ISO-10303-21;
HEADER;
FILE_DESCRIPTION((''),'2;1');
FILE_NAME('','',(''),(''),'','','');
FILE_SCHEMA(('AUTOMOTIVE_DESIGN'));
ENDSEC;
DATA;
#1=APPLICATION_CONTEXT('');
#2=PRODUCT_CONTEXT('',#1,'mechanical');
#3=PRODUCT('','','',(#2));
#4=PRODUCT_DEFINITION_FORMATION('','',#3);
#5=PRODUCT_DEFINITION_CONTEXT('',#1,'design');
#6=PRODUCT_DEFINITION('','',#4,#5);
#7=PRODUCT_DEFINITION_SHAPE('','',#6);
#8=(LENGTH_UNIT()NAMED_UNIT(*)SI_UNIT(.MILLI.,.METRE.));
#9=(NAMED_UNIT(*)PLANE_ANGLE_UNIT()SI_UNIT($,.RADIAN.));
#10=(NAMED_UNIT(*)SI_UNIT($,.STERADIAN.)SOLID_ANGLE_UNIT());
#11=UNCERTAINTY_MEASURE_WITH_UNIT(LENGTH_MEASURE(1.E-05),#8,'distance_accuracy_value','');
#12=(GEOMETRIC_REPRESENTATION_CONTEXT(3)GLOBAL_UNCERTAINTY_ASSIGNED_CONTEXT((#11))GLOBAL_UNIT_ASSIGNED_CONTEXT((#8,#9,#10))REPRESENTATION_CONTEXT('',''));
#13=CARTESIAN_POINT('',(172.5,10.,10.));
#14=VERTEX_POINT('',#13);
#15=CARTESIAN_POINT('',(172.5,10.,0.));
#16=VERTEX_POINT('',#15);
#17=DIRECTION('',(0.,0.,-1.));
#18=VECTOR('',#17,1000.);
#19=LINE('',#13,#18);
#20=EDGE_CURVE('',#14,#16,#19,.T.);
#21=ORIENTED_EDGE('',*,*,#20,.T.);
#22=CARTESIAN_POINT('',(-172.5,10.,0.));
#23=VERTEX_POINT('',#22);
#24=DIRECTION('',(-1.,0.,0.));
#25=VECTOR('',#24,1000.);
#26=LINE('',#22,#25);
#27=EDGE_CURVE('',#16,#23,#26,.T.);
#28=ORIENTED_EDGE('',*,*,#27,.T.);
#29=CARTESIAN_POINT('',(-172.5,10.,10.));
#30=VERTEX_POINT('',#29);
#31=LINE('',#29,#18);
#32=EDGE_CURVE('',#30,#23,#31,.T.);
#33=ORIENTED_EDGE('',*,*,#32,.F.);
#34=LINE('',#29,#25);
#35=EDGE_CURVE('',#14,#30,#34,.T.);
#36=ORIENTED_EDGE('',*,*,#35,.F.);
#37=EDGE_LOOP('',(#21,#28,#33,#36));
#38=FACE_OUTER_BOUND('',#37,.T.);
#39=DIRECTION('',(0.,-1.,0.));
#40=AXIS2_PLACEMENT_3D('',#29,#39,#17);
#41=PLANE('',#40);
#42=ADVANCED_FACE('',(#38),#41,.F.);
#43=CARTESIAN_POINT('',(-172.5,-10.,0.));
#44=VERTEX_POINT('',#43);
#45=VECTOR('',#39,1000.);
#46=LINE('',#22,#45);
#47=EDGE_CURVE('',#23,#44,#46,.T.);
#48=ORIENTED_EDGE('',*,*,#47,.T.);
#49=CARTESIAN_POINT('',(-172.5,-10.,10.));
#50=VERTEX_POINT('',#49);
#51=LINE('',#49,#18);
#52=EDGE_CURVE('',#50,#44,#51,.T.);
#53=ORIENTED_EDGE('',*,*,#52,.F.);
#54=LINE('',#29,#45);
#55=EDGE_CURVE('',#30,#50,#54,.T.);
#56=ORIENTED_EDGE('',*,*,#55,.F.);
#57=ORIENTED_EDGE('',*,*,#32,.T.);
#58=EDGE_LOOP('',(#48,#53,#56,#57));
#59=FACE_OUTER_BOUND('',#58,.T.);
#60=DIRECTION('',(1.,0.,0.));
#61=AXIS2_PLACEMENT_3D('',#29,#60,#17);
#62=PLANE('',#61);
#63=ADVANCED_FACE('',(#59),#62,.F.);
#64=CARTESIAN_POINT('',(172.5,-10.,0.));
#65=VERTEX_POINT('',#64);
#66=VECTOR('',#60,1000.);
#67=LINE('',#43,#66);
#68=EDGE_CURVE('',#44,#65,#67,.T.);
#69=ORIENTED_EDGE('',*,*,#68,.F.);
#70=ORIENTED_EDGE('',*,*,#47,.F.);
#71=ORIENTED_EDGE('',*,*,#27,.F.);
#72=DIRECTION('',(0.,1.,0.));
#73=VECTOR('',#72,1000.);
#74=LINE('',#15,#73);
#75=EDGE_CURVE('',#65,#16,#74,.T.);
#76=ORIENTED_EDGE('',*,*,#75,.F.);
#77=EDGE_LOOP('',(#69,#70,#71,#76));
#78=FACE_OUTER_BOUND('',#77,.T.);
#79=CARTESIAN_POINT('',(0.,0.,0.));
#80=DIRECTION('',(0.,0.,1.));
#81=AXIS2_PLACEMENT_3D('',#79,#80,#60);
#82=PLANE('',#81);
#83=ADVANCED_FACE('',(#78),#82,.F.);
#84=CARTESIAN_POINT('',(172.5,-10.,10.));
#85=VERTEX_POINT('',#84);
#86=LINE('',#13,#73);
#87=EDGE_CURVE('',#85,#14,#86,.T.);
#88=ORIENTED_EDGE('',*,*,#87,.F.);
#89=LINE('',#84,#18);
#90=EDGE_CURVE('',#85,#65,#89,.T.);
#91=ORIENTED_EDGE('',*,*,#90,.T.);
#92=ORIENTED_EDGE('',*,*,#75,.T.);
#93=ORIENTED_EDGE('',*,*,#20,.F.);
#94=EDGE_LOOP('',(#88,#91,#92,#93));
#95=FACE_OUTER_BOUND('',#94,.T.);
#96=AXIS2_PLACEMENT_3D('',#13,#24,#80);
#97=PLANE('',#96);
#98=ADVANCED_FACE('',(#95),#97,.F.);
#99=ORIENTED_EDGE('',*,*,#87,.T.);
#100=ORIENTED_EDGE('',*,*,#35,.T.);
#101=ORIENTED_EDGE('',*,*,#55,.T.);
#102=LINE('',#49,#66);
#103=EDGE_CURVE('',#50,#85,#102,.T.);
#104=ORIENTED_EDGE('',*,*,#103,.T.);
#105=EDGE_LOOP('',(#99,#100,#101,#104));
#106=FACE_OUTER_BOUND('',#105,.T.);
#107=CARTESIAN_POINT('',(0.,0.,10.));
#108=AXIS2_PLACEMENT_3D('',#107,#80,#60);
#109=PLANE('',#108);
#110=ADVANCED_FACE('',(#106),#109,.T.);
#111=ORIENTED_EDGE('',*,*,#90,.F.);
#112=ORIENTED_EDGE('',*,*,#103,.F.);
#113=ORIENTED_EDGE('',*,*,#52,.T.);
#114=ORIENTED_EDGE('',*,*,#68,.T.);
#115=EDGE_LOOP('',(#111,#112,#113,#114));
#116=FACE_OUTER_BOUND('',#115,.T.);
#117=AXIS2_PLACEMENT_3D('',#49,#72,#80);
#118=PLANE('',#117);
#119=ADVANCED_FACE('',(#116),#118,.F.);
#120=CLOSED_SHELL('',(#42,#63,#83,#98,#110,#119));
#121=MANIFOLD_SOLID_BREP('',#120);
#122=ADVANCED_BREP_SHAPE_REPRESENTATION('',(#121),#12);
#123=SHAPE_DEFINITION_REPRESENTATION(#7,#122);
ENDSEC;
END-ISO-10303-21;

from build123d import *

# Parameters (mm, degrees)
SKETCH1_W           = 345
SKETCH1_H           = 20
BOSS_EXTRUDE1_DEPTH = 10


with BuildPart() as part:
    # Sketch1 → Boss-Extrude1 (new body)
    with BuildSketch(Plane.XY):
        Rectangle(SKETCH1_W, SKETCH1_H)
    extrude(amount=BOSS_EXTRUDE1_DEPTH)


solid = part.part
